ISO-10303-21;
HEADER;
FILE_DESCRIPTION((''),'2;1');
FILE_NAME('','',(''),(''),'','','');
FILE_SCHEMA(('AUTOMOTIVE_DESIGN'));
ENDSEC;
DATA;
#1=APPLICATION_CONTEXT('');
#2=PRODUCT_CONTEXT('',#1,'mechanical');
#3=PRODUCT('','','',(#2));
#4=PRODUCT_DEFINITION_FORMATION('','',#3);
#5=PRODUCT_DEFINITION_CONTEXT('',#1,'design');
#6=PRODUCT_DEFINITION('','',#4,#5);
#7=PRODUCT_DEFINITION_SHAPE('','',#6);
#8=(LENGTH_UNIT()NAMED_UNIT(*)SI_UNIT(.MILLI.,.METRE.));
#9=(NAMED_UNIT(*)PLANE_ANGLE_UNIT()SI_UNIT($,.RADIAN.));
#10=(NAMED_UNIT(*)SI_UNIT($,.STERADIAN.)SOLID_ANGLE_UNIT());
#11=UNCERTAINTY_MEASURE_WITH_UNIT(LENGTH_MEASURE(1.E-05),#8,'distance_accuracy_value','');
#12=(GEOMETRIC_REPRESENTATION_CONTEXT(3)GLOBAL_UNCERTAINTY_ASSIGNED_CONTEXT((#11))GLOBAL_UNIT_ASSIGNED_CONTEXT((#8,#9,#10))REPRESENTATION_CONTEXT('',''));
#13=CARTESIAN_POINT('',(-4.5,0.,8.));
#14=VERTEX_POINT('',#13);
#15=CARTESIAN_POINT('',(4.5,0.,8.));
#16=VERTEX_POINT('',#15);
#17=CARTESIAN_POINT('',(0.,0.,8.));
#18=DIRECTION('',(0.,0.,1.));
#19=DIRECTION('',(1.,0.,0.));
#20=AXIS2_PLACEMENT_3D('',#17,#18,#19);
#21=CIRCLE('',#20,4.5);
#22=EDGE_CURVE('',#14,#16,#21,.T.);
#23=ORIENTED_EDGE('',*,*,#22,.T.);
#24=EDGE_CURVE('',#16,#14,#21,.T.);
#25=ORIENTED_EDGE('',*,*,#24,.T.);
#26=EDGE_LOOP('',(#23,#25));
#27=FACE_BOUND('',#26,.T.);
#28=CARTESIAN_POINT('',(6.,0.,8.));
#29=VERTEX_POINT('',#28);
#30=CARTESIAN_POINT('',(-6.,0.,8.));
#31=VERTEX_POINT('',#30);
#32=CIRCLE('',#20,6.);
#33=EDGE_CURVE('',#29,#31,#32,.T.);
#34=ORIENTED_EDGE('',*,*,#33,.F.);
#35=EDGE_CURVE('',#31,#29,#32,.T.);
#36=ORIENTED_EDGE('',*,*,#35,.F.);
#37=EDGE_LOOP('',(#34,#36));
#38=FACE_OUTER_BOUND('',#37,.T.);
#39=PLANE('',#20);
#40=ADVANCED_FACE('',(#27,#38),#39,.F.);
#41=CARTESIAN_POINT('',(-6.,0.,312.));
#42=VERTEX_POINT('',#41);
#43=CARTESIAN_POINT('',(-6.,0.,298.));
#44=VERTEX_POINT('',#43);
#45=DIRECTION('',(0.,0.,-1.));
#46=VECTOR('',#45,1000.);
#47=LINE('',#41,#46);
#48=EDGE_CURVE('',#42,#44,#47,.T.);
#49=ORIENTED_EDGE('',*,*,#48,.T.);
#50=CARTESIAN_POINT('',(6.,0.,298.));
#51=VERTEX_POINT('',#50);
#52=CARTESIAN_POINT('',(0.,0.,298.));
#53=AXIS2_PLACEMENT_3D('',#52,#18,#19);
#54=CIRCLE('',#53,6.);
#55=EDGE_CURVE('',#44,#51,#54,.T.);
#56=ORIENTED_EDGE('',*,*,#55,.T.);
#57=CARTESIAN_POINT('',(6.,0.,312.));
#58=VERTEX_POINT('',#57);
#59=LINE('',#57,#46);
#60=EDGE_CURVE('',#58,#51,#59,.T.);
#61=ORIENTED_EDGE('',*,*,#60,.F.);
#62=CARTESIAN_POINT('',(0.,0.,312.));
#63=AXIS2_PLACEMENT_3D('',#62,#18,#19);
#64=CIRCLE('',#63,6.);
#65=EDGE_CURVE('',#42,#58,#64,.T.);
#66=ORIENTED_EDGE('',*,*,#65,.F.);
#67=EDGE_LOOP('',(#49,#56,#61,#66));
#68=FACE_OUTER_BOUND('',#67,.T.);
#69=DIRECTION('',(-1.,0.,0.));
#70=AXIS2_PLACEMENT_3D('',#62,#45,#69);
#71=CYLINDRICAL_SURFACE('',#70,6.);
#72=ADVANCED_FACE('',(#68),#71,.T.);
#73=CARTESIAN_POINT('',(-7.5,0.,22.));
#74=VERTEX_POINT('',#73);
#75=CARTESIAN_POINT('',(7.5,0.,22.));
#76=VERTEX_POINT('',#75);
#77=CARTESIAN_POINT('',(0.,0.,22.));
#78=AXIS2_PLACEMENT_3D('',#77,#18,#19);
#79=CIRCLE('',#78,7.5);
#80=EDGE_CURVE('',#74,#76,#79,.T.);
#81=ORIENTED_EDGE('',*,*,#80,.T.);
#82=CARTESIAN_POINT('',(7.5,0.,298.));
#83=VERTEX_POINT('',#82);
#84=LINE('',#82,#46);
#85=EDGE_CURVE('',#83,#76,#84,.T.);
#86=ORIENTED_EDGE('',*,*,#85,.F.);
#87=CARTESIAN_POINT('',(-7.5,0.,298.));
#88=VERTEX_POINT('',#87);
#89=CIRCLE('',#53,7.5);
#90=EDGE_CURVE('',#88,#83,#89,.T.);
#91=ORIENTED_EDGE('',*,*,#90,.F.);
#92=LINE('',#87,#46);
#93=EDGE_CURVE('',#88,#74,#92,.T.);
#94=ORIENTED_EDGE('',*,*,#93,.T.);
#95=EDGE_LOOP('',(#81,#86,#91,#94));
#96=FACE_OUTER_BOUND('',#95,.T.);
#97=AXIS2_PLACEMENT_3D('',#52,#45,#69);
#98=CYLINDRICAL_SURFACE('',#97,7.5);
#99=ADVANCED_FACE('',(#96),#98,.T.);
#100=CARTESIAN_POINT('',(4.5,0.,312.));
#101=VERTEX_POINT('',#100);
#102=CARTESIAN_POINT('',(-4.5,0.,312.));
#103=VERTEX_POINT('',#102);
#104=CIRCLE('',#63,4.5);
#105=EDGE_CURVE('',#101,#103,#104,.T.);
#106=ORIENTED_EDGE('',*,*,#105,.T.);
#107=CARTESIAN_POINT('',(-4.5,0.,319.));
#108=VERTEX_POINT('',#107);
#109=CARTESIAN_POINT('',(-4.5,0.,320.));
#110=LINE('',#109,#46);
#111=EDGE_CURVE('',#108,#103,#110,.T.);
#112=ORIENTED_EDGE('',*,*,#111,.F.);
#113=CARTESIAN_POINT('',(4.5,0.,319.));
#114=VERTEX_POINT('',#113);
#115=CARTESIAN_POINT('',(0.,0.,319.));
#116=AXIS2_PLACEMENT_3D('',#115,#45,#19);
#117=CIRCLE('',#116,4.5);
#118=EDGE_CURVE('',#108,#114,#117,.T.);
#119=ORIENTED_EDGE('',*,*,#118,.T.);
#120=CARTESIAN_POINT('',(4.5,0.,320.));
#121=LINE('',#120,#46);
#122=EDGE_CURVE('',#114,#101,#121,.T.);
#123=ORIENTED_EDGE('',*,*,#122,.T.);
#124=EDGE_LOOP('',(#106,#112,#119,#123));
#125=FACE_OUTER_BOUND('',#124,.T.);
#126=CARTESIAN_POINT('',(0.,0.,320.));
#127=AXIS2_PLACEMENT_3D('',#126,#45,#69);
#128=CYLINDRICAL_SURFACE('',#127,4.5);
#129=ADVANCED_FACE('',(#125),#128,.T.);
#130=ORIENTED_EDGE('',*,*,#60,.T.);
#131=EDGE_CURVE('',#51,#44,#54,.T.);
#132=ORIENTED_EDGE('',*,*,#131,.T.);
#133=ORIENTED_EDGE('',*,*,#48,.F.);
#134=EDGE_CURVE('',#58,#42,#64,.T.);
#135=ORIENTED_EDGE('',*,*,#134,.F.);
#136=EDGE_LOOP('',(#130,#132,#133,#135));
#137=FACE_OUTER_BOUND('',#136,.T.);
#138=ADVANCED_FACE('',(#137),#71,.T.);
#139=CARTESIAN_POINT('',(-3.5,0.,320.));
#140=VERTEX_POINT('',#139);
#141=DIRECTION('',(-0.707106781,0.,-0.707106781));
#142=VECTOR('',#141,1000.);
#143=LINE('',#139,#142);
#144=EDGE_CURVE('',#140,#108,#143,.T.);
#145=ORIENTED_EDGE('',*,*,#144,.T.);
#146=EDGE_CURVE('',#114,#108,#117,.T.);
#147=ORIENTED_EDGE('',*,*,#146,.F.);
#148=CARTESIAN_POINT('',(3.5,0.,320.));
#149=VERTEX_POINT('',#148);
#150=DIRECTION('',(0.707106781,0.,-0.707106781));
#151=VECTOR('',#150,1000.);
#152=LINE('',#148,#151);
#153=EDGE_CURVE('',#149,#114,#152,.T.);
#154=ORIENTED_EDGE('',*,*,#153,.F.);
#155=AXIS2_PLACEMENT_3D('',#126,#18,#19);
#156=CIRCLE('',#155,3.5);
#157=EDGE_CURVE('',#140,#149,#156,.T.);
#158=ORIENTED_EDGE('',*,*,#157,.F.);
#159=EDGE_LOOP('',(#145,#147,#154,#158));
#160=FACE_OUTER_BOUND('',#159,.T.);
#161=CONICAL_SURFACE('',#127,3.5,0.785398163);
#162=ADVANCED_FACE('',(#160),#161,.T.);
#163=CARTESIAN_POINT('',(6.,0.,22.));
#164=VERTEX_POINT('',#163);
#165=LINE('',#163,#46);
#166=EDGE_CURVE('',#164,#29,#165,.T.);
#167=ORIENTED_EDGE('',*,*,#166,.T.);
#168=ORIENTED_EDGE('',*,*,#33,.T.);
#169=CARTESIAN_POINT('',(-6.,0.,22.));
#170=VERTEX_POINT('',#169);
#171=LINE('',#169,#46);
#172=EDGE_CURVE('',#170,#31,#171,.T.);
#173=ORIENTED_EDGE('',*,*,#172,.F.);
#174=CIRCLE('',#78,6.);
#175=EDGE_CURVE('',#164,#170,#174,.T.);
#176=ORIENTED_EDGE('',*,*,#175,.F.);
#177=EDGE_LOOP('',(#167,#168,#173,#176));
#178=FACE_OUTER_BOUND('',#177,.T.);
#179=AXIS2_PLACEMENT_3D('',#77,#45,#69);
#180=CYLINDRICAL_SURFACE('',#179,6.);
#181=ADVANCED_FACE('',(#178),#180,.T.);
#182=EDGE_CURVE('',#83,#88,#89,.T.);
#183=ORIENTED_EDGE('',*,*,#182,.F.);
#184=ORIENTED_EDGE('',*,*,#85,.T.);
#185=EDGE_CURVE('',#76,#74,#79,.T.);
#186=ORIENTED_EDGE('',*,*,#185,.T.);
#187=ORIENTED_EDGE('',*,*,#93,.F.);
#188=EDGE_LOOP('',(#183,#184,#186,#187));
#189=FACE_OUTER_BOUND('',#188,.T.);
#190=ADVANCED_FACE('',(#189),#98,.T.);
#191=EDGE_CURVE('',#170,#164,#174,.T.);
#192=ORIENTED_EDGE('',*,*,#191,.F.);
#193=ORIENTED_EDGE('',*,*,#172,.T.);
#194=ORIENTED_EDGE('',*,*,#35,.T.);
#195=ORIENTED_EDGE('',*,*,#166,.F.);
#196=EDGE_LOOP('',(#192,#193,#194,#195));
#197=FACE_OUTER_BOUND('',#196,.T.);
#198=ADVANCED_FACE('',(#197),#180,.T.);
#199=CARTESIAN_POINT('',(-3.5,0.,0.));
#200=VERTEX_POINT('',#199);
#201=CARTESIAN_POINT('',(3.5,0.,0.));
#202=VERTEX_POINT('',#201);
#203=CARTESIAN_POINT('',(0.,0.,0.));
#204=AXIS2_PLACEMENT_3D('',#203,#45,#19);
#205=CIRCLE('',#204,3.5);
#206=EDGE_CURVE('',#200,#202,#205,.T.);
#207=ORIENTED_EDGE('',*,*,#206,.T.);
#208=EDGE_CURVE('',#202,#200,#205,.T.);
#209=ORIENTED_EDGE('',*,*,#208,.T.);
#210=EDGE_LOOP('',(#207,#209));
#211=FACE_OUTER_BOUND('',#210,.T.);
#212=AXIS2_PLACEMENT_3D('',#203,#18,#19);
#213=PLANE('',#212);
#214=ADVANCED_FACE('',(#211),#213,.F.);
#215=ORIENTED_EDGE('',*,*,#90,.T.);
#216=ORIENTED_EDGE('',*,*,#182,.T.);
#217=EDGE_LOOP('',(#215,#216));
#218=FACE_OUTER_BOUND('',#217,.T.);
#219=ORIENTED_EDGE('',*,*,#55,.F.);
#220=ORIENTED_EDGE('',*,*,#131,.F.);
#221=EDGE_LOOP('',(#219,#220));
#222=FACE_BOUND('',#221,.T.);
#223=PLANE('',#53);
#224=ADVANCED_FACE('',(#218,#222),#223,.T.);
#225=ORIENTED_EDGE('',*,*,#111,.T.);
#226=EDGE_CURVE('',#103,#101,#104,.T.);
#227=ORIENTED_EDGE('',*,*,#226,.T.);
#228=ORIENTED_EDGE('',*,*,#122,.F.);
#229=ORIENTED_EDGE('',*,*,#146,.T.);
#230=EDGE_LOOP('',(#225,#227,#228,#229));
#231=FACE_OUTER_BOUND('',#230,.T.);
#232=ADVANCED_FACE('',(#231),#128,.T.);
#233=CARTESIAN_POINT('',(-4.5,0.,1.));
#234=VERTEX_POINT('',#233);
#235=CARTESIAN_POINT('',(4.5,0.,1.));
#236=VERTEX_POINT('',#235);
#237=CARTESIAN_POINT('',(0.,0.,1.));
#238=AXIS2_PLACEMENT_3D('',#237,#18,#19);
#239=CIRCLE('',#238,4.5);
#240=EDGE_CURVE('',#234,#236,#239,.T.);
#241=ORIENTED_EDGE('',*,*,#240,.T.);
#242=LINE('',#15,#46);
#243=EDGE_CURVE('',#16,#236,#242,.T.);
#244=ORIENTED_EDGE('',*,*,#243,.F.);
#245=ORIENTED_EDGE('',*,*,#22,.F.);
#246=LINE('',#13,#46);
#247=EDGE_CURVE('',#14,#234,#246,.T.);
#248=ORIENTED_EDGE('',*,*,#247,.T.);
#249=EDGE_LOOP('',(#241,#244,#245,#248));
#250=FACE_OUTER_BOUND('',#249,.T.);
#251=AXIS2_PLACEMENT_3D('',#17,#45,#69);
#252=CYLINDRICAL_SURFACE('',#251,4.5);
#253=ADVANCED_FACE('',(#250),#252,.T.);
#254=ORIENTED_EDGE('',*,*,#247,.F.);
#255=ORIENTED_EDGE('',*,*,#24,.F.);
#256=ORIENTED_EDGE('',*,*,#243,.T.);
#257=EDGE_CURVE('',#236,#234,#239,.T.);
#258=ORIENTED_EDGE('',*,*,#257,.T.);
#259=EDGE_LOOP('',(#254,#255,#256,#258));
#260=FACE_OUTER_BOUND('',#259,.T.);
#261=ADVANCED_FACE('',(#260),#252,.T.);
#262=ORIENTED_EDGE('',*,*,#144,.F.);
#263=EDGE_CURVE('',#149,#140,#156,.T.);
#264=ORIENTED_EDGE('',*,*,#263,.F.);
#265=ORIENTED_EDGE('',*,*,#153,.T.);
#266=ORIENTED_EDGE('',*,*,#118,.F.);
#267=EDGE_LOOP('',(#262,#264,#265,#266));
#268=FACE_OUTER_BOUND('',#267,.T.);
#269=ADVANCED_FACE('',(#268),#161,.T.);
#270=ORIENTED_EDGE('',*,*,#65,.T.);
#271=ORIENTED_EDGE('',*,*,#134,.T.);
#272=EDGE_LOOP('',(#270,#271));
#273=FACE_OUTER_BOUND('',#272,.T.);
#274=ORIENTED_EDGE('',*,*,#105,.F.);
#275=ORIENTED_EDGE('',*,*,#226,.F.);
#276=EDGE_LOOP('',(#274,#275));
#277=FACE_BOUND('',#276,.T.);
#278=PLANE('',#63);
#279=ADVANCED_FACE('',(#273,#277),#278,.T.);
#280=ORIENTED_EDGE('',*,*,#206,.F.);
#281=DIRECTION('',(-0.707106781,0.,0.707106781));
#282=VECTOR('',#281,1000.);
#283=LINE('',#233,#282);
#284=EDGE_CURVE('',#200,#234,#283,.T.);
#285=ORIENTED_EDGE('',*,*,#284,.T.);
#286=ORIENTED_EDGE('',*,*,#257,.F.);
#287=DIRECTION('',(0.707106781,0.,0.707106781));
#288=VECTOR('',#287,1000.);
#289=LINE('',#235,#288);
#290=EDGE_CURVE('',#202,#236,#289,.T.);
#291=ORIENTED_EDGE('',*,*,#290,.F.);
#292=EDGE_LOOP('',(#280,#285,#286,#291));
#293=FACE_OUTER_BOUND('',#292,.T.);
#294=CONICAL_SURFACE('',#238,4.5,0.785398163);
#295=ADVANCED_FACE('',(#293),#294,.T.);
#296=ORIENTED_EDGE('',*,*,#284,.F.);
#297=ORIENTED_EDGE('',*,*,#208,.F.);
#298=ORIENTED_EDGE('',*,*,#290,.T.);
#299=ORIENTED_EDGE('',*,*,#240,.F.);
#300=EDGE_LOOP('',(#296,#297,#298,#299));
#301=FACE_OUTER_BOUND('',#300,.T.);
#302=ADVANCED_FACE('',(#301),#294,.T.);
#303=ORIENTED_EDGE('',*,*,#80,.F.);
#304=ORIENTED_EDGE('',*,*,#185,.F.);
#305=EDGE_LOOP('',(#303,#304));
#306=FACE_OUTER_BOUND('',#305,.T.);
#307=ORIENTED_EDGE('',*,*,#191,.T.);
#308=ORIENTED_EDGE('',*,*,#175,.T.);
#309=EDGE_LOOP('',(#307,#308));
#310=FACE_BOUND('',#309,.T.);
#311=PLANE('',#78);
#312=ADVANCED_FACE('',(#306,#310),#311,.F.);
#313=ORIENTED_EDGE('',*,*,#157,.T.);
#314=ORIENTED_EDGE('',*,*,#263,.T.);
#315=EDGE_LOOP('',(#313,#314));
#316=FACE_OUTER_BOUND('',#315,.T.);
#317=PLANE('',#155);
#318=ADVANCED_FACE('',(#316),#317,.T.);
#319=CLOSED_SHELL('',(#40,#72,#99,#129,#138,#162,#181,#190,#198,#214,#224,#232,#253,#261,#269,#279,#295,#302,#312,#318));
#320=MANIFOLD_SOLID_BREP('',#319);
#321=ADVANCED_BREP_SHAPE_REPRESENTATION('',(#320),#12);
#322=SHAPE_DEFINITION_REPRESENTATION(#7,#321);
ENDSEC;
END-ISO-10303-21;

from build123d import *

# Parameters (mm, degrees)
SKETCH_1_R      = 4.5
EXTRUDE_1_DEPTH = 8
SKETCH_2_R      = 6
EXTRUDE_2_DEPTH = 14
SKETCH_3_R      = 7.5
EXTRUDE_3_DEPTH = 276
SKETCH_4_R      = 6
EXTRUDE_4_DEPTH = 14
SKETCH_5_R      = 4.5
EXTRUDE_5_DEPTH = 8
CHAMFER_1_SIZE  = 1


with BuildPart() as part:
    # 草图1 → 凸台-拉伸1 (new body)
    with BuildSketch(Plane.XY):
        Circle(SKETCH_1_R)
    extrude(amount=EXTRUDE_1_DEPTH)

    # 草图2 → 凸台-拉伸2 (add)
    with BuildSketch(Plane.XY.offset(8)):
        Circle(SKETCH_2_R)
    extrude(amount=EXTRUDE_2_DEPTH)

    # 草图3 → 凸台-拉伸3 (add)
    with BuildSketch(Plane.XY.offset(22)):
        Circle(SKETCH_3_R)
    extrude(amount=EXTRUDE_3_DEPTH)

    # 草图4 → 凸台-拉伸4 (add)
    with BuildSketch(Plane.XY.offset(298)):
        Circle(SKETCH_4_R)
    extrude(amount=EXTRUDE_4_DEPTH)

    # 草图5 → 凸台-拉伸5 (add)
    with BuildSketch(Plane.XY.offset(312)):
        Circle(SKETCH_5_R)
    extrude(amount=EXTRUDE_5_DEPTH)

    # 倒角1
    chamfer_1_edges = [part.edges().sort_by_distance(p)[0] for p in [
        (-4.5, 0, 0),
        (-4.5, 0, 320),
    ]]
    chamfer(chamfer_1_edges, length=CHAMFER_1_SIZE)


solid = part.part
